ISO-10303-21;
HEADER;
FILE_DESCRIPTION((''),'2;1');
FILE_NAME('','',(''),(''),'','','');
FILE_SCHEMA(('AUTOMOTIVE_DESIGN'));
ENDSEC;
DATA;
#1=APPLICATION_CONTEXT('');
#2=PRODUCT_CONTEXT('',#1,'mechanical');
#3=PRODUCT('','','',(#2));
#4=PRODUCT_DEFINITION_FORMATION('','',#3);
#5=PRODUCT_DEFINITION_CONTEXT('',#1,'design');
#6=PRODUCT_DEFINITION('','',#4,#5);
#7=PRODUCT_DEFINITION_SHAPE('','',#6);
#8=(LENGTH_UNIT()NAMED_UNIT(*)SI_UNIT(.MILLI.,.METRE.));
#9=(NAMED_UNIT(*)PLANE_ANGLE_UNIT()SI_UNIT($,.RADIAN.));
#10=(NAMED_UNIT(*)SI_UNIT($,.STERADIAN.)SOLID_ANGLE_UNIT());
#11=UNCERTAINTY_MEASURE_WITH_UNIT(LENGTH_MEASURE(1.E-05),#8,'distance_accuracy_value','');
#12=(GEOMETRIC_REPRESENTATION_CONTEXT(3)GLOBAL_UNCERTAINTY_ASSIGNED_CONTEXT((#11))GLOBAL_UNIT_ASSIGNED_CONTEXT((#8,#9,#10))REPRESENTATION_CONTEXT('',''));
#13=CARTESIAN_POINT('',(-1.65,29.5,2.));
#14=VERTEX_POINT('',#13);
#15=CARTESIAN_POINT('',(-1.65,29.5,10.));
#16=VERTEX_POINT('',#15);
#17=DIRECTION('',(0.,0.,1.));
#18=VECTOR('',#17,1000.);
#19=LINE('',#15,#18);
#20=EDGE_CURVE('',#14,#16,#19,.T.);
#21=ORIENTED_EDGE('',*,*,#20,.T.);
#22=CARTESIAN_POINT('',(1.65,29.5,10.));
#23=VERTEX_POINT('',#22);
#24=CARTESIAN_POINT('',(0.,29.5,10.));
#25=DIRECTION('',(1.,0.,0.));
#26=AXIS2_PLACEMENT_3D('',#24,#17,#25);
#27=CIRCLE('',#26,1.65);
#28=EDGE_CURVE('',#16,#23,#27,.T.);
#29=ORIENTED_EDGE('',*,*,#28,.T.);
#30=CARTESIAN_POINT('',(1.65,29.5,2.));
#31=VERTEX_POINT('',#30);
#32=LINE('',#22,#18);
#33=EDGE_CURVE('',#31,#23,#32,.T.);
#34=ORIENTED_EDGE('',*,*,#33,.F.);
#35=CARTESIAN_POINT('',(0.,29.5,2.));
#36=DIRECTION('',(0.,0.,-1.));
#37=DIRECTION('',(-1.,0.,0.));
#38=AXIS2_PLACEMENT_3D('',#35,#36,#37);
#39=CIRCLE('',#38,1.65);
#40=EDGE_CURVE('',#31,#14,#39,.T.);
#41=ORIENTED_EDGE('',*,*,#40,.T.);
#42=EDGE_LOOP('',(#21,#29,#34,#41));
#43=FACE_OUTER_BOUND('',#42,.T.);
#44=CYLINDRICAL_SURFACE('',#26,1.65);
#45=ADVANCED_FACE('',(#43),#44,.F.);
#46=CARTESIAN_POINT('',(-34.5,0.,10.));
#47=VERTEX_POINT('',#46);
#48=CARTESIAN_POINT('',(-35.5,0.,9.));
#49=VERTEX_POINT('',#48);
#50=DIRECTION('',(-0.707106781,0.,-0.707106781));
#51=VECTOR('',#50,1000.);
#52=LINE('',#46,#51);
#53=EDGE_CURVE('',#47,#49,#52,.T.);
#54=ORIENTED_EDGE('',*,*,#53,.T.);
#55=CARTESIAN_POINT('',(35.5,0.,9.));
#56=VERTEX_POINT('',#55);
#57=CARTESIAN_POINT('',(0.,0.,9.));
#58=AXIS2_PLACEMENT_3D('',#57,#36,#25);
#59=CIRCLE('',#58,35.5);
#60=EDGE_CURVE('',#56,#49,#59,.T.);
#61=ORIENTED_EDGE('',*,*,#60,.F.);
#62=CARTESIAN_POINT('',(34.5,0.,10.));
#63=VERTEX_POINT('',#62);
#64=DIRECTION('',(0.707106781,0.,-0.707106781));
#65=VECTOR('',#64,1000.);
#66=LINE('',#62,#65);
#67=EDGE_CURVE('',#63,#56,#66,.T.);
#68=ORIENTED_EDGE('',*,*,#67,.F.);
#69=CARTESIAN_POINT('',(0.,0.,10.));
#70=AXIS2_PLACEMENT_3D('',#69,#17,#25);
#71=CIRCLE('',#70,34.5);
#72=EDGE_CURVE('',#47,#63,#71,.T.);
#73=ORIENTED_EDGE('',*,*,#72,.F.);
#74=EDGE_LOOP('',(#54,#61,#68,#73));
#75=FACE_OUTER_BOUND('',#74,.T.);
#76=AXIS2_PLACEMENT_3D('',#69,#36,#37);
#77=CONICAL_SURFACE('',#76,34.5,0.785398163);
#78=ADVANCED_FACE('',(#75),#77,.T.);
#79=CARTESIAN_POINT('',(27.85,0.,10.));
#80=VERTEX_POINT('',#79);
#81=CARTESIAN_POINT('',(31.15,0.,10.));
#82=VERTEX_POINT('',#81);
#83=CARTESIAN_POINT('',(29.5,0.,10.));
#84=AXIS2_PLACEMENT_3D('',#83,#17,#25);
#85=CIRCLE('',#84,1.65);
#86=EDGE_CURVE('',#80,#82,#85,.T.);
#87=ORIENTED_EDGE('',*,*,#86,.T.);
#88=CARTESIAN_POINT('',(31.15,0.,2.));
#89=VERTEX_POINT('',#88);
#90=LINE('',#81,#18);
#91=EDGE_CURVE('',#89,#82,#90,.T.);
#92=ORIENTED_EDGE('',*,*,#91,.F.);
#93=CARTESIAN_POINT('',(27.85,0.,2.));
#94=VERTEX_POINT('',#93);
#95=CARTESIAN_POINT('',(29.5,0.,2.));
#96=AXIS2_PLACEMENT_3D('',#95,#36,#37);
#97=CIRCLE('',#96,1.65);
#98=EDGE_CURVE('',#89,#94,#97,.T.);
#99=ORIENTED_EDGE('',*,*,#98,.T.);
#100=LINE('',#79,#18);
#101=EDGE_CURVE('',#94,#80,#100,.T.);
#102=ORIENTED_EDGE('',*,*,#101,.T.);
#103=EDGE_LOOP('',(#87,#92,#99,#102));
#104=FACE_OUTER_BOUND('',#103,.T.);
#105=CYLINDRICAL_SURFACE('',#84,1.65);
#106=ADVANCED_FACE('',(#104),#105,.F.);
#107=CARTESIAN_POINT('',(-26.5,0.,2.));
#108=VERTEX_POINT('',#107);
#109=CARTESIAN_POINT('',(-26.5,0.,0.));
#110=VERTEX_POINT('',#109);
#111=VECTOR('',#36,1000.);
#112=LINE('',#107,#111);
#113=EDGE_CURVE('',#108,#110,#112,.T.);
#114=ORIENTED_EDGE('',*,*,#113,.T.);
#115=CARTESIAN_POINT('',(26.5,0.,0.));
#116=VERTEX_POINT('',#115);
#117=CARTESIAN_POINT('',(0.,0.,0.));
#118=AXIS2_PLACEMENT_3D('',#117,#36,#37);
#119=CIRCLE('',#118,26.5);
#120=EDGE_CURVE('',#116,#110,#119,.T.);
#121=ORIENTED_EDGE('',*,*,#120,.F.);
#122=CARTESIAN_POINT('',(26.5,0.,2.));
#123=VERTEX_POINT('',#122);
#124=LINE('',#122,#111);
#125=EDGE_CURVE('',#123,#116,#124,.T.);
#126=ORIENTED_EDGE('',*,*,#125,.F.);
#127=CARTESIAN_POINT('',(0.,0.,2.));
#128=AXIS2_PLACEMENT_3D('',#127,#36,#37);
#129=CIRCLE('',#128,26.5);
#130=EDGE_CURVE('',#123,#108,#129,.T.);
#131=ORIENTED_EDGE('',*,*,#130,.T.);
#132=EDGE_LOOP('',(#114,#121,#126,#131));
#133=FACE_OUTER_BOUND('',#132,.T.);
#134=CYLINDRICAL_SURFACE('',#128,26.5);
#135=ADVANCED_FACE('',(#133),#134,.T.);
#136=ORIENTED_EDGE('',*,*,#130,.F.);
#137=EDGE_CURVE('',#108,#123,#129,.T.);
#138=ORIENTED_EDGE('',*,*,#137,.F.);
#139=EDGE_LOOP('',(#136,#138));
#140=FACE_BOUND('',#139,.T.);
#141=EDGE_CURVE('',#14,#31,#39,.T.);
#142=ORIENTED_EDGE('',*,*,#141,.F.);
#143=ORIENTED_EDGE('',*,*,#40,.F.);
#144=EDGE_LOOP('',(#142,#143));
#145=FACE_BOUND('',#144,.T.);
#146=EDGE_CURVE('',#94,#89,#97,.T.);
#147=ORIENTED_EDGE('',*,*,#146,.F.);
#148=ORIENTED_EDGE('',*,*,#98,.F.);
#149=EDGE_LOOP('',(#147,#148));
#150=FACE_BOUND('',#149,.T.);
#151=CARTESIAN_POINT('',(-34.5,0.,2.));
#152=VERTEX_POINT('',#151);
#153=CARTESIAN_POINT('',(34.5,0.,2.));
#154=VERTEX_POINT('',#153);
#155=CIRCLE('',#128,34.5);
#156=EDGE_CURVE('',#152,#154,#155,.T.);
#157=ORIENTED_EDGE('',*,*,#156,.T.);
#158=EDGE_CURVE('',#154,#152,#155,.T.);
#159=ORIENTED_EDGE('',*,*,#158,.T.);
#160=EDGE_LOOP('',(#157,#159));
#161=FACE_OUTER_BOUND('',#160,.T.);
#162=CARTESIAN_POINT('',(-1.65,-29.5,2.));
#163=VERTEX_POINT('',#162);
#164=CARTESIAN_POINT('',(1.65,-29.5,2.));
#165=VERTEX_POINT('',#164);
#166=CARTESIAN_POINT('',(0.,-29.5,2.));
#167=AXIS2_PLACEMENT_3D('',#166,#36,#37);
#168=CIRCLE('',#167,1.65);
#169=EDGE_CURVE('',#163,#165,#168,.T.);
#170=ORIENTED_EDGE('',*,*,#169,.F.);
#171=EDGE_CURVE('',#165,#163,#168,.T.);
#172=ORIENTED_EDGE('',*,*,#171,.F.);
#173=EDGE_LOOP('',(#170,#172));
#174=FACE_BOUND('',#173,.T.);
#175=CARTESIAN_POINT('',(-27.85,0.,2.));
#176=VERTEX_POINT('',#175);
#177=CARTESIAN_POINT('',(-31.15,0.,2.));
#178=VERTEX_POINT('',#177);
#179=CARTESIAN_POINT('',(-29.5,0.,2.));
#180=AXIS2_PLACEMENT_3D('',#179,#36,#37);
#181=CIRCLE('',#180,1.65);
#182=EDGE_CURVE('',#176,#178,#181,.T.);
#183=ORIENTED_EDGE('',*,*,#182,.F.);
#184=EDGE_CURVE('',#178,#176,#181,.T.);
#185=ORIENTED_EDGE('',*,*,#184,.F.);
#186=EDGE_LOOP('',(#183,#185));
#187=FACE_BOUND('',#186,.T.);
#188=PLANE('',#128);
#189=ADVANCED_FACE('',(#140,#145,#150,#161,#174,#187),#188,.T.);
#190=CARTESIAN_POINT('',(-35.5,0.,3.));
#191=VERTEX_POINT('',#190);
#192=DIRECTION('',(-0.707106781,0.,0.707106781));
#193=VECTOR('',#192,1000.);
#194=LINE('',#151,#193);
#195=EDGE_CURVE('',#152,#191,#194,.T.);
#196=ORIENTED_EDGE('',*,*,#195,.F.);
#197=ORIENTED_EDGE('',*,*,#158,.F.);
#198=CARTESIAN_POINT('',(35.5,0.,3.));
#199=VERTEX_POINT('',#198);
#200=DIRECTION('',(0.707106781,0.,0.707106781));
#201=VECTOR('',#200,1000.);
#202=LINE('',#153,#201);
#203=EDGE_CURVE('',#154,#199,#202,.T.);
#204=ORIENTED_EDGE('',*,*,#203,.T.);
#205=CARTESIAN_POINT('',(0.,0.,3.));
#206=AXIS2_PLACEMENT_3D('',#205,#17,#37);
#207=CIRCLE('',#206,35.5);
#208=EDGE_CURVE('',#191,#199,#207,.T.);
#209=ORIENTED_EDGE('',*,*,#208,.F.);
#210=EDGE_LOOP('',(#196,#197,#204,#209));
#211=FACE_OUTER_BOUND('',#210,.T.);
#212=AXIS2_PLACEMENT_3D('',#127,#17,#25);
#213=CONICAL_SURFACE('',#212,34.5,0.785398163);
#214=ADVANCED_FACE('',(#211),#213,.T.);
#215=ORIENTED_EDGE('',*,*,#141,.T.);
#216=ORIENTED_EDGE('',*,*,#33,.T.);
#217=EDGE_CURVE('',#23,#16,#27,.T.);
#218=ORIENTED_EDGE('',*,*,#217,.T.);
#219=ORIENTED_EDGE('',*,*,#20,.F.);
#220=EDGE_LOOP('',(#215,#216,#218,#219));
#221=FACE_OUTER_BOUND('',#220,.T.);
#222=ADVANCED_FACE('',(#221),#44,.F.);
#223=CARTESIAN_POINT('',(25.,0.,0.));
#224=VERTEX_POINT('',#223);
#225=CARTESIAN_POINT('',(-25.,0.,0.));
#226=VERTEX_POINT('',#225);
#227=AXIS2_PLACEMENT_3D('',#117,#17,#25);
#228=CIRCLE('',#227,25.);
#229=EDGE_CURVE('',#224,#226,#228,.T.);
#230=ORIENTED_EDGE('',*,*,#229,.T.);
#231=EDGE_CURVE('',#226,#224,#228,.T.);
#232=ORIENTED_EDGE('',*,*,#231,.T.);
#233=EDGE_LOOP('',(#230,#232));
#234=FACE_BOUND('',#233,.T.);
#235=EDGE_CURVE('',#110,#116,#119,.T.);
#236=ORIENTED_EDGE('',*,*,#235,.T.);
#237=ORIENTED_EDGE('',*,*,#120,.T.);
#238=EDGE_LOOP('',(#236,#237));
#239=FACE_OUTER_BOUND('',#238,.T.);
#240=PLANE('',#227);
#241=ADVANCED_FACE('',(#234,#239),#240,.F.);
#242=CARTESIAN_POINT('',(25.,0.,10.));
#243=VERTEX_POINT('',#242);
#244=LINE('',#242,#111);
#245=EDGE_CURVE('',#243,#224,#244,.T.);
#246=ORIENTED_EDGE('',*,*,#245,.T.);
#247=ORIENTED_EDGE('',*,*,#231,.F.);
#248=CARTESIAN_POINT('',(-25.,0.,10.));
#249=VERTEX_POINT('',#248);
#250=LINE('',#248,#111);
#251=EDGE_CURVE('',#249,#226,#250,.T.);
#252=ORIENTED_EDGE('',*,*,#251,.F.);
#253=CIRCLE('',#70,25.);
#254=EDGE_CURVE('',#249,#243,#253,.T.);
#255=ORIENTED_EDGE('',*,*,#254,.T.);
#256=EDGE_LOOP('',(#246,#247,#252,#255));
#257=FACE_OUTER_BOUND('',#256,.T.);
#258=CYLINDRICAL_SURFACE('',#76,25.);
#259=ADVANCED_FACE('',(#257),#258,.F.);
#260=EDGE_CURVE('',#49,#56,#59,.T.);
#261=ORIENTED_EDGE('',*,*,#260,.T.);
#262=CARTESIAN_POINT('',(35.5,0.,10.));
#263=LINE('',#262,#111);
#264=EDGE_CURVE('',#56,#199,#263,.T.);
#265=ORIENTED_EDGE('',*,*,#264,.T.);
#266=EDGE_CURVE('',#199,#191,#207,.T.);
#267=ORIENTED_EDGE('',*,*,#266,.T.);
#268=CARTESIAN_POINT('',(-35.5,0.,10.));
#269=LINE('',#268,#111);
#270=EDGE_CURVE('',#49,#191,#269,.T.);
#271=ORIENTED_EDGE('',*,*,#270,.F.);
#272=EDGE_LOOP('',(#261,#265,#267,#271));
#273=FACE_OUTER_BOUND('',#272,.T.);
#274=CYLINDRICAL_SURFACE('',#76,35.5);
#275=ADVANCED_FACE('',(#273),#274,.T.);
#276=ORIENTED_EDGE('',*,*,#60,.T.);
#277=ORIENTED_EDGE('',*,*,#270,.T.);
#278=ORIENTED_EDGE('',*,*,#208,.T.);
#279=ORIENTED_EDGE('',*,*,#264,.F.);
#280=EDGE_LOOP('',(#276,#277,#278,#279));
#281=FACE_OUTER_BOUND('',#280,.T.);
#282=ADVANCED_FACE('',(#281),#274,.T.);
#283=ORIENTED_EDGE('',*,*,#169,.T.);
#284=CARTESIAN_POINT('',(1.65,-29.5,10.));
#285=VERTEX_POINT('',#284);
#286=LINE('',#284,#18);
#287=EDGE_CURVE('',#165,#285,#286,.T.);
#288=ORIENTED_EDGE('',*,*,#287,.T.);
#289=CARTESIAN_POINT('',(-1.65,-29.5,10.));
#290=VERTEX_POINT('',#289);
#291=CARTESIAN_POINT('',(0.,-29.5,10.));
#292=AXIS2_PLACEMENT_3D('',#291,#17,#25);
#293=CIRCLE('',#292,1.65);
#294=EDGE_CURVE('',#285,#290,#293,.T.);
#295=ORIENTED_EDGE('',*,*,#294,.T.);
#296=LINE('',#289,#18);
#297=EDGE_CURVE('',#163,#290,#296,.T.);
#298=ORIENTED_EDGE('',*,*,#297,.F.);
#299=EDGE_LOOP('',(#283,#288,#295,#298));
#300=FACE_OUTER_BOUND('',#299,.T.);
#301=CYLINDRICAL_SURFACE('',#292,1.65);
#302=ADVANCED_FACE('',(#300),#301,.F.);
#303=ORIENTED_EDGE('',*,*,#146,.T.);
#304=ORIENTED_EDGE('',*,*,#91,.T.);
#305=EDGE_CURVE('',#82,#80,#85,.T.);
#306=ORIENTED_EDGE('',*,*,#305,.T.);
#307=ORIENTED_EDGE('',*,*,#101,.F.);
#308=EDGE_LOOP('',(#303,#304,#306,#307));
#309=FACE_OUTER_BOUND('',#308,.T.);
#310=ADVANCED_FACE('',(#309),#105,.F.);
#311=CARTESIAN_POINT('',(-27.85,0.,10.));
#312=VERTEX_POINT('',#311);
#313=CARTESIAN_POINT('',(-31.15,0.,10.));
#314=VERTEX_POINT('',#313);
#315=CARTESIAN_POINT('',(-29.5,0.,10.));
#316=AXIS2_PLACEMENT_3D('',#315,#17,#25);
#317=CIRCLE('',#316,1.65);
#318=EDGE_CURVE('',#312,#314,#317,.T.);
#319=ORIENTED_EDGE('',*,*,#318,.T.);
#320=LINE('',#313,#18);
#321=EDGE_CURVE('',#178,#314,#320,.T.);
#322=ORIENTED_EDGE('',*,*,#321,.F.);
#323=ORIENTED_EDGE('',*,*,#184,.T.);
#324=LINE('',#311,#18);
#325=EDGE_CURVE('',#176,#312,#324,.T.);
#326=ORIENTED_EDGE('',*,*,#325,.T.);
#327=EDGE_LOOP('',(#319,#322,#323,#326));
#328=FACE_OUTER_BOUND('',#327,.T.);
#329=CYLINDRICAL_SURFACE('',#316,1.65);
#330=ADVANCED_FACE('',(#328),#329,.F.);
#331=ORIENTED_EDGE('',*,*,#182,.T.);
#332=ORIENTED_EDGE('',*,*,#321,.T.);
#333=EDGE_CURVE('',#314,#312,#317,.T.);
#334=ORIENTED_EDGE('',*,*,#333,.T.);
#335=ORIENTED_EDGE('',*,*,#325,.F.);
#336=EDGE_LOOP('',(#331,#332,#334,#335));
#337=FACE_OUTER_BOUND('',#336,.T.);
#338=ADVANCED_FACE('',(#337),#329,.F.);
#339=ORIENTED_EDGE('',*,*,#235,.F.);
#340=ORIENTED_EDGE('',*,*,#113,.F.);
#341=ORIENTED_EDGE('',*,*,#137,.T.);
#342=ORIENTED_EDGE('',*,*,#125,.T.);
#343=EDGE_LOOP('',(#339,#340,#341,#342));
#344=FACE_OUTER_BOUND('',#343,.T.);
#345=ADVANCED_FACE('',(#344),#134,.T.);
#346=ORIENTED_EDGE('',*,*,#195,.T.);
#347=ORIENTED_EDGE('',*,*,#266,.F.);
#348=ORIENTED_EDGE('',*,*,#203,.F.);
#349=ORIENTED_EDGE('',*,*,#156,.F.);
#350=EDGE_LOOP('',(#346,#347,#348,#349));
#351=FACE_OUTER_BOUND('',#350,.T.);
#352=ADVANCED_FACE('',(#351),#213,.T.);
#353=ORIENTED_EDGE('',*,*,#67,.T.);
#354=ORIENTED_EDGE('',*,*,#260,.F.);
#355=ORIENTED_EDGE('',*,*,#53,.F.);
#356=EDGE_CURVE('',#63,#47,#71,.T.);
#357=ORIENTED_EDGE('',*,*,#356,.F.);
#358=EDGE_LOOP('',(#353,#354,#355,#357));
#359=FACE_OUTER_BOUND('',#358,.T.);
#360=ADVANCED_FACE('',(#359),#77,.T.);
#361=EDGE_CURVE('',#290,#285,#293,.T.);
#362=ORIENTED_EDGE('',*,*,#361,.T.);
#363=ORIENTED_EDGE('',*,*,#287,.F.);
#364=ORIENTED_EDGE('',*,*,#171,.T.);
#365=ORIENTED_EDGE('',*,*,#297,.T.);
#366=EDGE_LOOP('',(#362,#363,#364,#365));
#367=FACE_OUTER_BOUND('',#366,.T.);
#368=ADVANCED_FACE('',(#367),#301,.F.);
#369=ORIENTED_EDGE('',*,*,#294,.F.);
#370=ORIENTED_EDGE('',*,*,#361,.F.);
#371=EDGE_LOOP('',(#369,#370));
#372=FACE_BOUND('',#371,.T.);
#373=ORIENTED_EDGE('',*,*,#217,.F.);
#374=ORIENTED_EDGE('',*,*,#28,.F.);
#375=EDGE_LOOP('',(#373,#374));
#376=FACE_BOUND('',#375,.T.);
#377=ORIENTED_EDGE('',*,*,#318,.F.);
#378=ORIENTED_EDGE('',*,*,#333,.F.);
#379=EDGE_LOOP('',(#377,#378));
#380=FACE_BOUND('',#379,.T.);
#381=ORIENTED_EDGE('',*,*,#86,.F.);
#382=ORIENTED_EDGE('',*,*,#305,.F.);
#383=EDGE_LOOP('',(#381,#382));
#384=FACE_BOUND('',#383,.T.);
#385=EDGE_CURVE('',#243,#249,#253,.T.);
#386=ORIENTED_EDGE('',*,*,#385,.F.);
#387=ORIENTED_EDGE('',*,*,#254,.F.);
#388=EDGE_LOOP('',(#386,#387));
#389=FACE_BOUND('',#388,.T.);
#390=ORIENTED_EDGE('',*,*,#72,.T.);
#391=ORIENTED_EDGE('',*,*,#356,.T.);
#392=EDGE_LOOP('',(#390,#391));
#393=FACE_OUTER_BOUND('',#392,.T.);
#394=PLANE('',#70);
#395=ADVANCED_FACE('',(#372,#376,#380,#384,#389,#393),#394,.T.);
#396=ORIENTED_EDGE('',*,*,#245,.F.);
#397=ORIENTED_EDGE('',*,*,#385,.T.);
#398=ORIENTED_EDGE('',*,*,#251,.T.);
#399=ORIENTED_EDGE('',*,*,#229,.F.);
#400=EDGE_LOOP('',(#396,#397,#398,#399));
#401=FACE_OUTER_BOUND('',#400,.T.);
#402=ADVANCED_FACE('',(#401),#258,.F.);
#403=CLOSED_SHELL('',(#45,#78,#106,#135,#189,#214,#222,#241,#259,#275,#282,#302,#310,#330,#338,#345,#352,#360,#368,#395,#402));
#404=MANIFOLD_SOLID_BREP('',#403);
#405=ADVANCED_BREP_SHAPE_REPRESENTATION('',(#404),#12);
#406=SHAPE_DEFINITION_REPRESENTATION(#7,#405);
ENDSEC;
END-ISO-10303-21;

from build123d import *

# Parameters (mm, degrees)
SKETCH1_R           = 35.5
SKETCH1_R_2         = 25
BOSS_EXTRUDE1_DEPTH = 10
SKETCH2_R           = 1.25
CUT_EXTRUDE1_DEPTH  = 52.190819489
SKETCH3_R           = 35.5
SKETCH3_R_2         = 26.5
CUT_EXTRUDE2_DEPTH  = 2
M4_TAPPED_HOLE1_D   = 3.3
CHAMFER1_SIZE       = 1


with BuildPart() as part:
    # Sketch1 → Boss-Extrude1 (new body)
    with BuildSketch(Plane.XY):
        Circle(SKETCH1_R)
        Circle(SKETCH1_R_2, mode=Mode.SUBTRACT)
    extrude(amount=BOSS_EXTRUDE1_DEPTH)

    # Sketch2 → Cut-Extrude1 (cut, through all)
    with BuildSketch(Plane.XY.offset(10)):
        with Locations((0, 29.5)):
            Circle(SKETCH2_R)
        with Locations((29.5, 0)):
            Circle(SKETCH2_R)
        with Locations((0, -29.5)):
            Circle(SKETCH2_R)
        with Locations((-29.5, 0)):
            Circle(SKETCH2_R)
    extrude(amount=-CUT_EXTRUDE1_DEPTH, mode=Mode.SUBTRACT)

    # Sketch3 → Cut-Extrude2 (cut)
    with BuildSketch(Plane(origin=(0, 0, 0), x_dir=(-1, 0, 0), z_dir=(0, 0, -1))):
        Circle(SKETCH3_R)
        Circle(SKETCH3_R_2, mode=Mode.SUBTRACT)
    extrude(amount=-CUT_EXTRUDE2_DEPTH, mode=Mode.SUBTRACT)

    # M4 Tapped Hole1 (through all)
    with Locations(Plane.XY.offset(10)):
        with Locations((0, -29.5), (-29.5, 0), (0, 29.5), (29.5, 0)):
            Hole(M4_TAPPED_HOLE1_D / 2)

    # Chamfer1
    chamfer1_edges = [part.edges().sort_by_distance(p)[0] for p in [
        (-35.5, 0, 2),
        (-35.5, 0, 10),
    ]]
    chamfer(chamfer1_edges, length=CHAMFER1_SIZE)


solid = part.part
